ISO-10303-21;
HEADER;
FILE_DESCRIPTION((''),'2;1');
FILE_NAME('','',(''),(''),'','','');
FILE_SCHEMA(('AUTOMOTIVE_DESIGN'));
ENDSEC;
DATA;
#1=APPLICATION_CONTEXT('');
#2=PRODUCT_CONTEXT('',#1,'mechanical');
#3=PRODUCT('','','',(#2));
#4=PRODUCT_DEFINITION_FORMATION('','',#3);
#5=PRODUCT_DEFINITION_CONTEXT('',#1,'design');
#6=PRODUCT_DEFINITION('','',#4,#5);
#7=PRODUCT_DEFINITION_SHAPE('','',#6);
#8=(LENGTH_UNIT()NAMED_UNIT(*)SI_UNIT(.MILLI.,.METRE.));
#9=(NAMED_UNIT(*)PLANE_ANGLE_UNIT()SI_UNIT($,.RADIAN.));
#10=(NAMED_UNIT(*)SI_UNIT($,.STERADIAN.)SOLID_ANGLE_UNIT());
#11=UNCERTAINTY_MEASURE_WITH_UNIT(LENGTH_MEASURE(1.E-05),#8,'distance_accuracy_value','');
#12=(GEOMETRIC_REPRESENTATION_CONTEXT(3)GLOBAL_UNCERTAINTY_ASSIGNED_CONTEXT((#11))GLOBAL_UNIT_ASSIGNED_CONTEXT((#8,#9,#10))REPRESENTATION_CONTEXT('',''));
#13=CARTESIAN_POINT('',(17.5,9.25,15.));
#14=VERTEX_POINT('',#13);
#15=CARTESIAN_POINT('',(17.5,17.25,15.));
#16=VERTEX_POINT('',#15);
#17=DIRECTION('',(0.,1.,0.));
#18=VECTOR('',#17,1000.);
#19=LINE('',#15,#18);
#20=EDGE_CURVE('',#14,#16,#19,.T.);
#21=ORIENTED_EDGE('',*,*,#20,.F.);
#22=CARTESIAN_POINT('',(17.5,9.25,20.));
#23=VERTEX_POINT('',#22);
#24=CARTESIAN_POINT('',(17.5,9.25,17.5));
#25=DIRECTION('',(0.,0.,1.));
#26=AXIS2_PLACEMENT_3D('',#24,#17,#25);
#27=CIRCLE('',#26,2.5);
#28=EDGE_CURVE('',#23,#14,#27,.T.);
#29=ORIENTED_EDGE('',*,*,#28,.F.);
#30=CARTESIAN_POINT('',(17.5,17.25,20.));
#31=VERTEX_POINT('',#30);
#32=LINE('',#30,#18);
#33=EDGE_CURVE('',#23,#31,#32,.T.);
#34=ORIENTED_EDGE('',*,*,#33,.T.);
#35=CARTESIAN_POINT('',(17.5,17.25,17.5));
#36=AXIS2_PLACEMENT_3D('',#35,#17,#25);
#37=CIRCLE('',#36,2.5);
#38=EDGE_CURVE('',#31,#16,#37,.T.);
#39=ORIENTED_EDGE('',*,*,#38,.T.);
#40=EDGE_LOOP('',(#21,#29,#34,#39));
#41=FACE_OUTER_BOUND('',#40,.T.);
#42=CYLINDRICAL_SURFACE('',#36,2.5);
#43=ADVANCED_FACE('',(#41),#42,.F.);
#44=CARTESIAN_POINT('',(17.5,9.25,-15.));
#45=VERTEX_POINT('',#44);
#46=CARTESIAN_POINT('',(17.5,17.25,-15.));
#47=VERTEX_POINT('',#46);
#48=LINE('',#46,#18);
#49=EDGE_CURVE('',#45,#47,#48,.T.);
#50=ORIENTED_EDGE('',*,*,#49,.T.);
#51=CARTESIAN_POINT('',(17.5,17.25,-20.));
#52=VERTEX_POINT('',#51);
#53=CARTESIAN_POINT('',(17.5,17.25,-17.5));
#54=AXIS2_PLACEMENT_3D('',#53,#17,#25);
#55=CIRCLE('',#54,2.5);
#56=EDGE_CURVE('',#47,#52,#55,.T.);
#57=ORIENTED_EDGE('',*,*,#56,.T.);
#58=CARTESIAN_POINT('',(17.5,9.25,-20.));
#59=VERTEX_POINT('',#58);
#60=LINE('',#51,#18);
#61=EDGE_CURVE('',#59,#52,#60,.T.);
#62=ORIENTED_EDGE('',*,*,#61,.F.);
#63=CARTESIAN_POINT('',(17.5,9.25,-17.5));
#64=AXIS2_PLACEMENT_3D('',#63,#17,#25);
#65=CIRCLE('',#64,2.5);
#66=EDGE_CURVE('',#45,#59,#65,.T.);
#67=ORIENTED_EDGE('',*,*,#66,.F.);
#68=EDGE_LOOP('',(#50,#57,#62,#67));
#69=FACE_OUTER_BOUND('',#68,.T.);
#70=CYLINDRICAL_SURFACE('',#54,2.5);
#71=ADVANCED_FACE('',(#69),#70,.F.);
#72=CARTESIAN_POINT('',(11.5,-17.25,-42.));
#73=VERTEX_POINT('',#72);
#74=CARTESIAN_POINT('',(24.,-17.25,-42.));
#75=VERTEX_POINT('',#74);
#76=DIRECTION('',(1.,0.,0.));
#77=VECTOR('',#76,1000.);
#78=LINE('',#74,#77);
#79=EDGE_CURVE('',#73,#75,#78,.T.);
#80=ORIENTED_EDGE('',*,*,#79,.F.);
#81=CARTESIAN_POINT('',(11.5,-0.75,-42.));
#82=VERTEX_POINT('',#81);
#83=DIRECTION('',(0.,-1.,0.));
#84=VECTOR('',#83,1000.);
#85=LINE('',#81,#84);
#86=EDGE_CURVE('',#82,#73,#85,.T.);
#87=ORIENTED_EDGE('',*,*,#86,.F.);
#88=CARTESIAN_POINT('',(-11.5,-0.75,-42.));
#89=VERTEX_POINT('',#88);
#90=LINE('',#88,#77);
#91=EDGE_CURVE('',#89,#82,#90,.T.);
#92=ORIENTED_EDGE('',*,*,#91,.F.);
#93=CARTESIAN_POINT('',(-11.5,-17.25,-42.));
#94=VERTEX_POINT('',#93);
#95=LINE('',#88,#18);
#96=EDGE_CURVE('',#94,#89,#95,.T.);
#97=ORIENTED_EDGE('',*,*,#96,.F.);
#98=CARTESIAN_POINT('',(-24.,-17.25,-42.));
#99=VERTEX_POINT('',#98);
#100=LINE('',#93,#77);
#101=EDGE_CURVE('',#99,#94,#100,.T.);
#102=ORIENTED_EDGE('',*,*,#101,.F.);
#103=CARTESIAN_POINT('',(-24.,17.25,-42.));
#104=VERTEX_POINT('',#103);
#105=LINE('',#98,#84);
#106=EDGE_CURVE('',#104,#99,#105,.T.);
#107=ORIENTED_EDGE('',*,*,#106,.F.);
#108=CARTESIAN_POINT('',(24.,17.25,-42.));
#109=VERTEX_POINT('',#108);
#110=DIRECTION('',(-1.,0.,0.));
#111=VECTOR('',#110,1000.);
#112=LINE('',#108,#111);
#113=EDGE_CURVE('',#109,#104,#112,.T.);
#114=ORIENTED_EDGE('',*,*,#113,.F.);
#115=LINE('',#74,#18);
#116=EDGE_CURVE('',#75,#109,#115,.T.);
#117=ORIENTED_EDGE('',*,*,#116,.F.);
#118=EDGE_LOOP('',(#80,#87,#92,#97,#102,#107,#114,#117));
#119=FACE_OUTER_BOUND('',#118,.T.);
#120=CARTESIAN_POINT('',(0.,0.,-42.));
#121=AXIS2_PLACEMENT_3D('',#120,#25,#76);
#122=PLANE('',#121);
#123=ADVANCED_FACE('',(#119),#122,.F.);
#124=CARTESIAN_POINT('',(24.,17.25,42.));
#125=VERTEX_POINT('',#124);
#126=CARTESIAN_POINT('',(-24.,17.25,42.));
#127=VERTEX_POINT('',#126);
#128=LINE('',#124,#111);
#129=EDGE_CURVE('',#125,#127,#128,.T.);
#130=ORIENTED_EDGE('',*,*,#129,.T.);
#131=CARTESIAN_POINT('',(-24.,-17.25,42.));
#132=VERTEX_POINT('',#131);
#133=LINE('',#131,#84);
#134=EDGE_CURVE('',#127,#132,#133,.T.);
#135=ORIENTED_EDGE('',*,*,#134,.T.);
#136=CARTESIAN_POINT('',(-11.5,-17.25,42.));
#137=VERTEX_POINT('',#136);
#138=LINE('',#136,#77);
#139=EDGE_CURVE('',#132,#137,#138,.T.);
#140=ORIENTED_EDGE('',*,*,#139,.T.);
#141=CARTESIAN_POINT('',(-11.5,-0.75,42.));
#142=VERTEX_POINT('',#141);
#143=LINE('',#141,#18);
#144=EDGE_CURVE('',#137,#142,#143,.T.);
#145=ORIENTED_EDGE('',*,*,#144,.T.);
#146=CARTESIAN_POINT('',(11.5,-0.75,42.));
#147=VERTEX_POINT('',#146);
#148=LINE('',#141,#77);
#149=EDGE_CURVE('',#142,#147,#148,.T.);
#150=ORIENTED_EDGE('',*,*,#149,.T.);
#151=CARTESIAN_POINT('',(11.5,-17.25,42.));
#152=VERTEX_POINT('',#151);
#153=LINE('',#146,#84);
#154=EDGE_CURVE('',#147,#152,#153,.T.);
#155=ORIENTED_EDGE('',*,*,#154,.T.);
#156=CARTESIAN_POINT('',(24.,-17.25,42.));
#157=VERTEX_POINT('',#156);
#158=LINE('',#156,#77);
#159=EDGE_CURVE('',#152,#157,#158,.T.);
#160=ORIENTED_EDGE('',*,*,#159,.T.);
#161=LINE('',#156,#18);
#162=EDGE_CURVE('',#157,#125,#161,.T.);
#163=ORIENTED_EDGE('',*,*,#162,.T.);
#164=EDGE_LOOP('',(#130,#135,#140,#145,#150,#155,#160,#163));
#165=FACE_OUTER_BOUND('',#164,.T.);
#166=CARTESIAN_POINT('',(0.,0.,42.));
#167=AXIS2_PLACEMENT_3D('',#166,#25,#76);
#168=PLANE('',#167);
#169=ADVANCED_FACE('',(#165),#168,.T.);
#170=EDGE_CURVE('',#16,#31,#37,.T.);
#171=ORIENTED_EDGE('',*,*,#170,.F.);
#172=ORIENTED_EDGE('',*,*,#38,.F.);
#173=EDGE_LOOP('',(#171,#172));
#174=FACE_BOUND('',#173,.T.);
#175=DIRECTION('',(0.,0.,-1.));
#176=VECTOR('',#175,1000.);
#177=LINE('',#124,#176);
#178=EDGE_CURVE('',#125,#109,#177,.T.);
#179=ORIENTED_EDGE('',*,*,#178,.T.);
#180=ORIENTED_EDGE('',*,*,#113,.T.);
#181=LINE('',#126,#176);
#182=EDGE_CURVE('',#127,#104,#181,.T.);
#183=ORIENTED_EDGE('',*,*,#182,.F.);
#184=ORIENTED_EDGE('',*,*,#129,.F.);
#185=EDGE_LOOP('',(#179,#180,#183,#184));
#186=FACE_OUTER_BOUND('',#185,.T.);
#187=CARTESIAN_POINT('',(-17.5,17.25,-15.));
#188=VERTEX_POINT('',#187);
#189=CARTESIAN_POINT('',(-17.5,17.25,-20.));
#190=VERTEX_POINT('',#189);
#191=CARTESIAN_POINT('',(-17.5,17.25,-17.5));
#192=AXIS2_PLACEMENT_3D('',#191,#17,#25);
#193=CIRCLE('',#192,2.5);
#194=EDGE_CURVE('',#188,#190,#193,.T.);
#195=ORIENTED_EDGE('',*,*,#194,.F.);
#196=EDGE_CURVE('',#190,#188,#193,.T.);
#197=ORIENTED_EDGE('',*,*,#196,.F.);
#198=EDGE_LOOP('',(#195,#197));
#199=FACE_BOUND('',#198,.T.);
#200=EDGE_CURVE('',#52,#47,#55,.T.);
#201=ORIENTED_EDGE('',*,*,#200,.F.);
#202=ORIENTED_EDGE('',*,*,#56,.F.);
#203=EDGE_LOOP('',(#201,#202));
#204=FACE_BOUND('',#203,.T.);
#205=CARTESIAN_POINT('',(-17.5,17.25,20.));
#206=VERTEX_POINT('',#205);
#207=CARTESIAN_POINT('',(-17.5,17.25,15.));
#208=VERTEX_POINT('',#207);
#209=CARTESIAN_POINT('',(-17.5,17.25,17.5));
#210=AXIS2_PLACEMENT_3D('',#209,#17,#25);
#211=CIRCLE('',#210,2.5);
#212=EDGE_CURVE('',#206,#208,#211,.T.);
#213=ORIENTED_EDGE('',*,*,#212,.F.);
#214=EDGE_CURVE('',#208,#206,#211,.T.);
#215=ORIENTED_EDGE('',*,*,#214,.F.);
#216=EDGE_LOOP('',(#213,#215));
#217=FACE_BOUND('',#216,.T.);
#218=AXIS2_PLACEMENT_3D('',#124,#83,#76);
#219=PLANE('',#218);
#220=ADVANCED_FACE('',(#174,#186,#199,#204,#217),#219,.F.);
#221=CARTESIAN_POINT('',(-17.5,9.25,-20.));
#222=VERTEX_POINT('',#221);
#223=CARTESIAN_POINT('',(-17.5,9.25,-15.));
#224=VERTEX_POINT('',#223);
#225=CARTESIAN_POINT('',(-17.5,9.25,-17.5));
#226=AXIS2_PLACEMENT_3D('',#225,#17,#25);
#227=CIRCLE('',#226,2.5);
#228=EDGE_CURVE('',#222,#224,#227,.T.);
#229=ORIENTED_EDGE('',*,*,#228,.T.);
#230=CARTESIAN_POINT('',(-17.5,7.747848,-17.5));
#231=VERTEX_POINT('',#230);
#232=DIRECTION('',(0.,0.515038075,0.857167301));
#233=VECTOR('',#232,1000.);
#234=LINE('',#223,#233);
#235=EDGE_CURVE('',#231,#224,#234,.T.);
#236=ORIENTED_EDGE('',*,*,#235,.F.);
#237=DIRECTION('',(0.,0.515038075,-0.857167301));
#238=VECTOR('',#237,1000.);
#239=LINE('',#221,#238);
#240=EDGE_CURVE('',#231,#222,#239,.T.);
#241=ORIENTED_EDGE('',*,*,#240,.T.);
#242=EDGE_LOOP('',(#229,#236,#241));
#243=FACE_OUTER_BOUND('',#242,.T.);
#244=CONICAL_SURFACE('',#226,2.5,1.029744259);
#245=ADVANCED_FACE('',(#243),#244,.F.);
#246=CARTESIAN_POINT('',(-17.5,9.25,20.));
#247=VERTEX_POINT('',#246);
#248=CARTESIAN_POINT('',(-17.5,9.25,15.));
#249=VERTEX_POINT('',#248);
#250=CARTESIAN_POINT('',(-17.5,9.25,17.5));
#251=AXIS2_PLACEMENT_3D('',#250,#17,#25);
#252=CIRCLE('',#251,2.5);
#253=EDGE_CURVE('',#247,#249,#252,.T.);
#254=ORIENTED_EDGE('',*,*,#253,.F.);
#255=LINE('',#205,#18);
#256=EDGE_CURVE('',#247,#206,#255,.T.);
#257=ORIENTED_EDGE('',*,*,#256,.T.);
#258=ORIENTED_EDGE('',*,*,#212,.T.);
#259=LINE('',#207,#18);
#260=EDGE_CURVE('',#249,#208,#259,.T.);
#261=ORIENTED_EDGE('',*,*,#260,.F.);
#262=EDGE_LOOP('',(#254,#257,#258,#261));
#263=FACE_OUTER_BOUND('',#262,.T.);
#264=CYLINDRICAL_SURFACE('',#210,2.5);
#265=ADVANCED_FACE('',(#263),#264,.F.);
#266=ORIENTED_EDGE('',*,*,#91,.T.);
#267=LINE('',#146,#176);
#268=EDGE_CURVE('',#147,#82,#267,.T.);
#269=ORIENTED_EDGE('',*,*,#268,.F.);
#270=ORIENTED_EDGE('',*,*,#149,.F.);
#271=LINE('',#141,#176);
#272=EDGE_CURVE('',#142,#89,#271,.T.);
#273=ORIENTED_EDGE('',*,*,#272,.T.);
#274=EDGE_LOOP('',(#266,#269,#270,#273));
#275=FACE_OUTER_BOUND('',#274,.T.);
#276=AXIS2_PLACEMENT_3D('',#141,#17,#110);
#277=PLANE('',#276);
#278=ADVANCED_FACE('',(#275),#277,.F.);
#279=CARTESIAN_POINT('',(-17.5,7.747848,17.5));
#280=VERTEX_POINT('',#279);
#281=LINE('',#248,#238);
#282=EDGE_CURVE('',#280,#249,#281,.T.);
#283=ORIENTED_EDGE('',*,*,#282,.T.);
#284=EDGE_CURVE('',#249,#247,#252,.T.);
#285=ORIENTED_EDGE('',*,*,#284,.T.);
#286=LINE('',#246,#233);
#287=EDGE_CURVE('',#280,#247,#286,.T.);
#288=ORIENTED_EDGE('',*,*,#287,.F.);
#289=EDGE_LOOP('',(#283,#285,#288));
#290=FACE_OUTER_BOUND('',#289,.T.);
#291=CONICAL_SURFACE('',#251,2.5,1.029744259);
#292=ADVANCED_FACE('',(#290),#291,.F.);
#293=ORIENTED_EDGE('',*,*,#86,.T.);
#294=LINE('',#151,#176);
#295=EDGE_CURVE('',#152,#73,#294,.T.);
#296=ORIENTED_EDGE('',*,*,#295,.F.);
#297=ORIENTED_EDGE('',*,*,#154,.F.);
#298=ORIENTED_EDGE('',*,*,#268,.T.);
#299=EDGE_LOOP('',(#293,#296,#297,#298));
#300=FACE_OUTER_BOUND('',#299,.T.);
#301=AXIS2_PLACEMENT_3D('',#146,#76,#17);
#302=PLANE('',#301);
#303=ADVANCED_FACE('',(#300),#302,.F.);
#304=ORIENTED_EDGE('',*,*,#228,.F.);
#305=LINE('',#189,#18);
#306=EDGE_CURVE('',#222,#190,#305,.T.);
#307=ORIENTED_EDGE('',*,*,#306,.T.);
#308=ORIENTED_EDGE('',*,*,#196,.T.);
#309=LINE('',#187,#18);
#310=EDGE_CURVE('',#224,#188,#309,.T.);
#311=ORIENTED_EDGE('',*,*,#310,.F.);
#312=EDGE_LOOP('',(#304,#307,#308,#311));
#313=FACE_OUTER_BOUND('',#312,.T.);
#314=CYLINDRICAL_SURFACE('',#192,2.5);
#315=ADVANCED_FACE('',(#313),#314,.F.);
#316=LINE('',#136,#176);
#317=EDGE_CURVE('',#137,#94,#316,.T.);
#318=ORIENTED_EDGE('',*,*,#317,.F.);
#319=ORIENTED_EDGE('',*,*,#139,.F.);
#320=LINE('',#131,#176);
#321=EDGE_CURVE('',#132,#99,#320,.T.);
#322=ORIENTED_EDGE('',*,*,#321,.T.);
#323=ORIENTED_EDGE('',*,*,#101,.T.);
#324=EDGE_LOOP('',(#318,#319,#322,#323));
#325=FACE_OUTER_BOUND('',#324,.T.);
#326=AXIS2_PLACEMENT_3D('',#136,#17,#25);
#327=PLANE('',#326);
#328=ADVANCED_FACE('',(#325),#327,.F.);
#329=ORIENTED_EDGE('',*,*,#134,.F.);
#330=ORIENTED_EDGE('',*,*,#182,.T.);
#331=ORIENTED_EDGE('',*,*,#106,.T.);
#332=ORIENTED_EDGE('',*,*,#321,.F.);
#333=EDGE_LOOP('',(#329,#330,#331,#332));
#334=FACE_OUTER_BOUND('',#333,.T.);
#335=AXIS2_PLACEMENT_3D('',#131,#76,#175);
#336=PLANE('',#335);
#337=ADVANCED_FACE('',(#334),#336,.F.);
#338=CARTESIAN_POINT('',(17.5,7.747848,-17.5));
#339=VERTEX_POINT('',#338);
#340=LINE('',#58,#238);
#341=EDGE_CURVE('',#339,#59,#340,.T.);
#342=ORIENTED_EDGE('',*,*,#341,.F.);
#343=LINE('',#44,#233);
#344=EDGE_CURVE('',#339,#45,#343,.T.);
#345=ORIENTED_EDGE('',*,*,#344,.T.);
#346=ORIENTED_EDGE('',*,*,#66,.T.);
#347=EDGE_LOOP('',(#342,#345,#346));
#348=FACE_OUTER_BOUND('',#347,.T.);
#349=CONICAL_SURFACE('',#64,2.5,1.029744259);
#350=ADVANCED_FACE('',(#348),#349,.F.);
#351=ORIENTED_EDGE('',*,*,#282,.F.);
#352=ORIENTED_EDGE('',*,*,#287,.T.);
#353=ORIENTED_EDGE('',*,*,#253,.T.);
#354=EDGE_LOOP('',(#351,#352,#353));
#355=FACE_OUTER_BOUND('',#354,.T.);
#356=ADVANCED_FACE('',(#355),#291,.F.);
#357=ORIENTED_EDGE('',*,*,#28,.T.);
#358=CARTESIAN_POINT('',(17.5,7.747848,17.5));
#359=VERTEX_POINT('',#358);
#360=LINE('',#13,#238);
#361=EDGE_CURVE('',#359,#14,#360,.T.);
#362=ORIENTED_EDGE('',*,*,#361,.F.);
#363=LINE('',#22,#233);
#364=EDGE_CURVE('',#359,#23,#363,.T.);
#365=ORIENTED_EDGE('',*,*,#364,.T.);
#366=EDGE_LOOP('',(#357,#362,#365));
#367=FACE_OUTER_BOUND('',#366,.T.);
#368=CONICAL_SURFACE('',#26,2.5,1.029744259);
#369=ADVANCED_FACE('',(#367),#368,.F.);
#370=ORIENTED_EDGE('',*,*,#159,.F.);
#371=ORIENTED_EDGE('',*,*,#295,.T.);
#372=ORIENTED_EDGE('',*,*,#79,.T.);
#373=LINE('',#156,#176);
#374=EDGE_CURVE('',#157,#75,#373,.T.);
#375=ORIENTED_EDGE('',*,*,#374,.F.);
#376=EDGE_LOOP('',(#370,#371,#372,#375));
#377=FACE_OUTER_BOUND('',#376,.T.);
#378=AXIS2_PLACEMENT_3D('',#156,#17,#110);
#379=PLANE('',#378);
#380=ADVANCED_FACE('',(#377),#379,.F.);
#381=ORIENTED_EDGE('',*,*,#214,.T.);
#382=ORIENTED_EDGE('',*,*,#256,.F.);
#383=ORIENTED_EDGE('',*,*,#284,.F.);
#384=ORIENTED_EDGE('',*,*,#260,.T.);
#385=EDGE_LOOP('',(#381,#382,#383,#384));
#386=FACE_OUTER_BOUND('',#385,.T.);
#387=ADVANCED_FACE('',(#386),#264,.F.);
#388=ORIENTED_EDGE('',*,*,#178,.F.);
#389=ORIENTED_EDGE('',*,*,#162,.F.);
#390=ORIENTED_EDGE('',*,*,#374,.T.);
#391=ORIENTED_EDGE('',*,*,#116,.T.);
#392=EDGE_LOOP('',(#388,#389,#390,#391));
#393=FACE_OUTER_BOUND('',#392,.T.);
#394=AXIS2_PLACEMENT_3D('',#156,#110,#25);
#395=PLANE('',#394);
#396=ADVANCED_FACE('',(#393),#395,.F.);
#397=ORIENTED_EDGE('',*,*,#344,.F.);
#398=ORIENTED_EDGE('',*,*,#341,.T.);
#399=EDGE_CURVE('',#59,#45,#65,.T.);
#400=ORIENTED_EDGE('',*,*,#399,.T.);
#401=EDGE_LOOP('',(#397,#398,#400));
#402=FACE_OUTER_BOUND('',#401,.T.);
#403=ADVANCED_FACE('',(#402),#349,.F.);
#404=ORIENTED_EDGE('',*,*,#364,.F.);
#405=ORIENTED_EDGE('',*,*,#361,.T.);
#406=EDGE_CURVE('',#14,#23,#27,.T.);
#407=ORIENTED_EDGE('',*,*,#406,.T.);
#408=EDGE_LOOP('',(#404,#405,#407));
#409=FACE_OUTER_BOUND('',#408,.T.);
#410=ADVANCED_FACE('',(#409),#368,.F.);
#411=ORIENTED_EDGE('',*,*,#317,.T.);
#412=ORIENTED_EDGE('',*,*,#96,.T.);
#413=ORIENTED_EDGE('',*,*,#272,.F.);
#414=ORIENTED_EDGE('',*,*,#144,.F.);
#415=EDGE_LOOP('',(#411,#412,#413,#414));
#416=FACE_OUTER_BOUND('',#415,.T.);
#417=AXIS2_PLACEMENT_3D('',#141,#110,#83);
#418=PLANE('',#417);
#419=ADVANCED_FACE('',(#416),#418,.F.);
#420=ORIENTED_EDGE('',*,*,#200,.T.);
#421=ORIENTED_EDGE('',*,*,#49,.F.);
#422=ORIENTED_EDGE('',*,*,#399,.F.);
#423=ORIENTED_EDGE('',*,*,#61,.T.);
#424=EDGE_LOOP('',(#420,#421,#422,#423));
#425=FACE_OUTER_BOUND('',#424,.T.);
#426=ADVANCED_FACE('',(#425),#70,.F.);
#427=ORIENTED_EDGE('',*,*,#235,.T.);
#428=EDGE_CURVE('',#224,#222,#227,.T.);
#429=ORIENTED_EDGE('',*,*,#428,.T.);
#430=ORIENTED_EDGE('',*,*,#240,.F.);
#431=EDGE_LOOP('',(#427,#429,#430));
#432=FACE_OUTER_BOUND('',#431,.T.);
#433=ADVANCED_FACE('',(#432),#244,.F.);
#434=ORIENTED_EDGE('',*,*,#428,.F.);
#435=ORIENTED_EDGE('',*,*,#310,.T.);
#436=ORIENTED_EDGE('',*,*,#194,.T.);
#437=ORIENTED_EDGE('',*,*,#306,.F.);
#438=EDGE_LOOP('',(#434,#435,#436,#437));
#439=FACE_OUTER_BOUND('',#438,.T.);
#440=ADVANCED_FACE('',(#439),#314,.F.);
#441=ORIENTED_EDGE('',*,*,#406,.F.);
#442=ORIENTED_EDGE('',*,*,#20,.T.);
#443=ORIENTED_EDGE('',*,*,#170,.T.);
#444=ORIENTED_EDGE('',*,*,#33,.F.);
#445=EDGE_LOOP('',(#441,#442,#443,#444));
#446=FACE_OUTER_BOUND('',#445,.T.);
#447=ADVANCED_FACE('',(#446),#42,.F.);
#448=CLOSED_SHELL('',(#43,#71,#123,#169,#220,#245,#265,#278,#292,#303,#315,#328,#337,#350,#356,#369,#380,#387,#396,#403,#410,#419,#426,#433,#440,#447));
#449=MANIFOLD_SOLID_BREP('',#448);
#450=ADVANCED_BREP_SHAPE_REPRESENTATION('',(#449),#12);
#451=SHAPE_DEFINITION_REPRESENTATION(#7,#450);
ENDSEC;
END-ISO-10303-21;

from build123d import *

# Parameters (mm, degrees)
EXTRUDE_1_DEPTH        = 42
HOLE_WIZARD_M6_1_D     = 5
HOLE_WIZARD_M6_1_DEPTH = 8
HOLE_WIZARD_M6_1_TIP   = 1.502151548


with BuildPart() as part:
    # 草图1 → 凸台-拉伸1 (new, symmetric)
    with BuildSketch(Plane.XY):
        Polygon((-11.5, -17.25), (-24, -17.25), (-24, 17.25), (24, 17.25), (24, -17.25), (11.5, -17.25), (11.5, -0.75), (-11.5, -0.75), align=None)
    extrude(amount=EXTRUDE_1_DEPTH, both=True)

    # M6 螺纹孔1
    with Locations(Plane(origin=(0, 17.25, 0), x_dir=(1, 0, 0), z_dir=(0, 1, 0))):
        with Locations((-17.5, 17.5), (17.5, 17.5), (17.5, -17.5), (-17.5, -17.5)):
            Hole(HOLE_WIZARD_M6_1_D / 2, depth=HOLE_WIZARD_M6_1_DEPTH)
            with Locations((0, 0, -(HOLE_WIZARD_M6_1_DEPTH + HOLE_WIZARD_M6_1_TIP / 2))):  # 118° drill point
                Cone(0, HOLE_WIZARD_M6_1_D / 2, HOLE_WIZARD_M6_1_TIP, mode=Mode.SUBTRACT)


solid = part.part
